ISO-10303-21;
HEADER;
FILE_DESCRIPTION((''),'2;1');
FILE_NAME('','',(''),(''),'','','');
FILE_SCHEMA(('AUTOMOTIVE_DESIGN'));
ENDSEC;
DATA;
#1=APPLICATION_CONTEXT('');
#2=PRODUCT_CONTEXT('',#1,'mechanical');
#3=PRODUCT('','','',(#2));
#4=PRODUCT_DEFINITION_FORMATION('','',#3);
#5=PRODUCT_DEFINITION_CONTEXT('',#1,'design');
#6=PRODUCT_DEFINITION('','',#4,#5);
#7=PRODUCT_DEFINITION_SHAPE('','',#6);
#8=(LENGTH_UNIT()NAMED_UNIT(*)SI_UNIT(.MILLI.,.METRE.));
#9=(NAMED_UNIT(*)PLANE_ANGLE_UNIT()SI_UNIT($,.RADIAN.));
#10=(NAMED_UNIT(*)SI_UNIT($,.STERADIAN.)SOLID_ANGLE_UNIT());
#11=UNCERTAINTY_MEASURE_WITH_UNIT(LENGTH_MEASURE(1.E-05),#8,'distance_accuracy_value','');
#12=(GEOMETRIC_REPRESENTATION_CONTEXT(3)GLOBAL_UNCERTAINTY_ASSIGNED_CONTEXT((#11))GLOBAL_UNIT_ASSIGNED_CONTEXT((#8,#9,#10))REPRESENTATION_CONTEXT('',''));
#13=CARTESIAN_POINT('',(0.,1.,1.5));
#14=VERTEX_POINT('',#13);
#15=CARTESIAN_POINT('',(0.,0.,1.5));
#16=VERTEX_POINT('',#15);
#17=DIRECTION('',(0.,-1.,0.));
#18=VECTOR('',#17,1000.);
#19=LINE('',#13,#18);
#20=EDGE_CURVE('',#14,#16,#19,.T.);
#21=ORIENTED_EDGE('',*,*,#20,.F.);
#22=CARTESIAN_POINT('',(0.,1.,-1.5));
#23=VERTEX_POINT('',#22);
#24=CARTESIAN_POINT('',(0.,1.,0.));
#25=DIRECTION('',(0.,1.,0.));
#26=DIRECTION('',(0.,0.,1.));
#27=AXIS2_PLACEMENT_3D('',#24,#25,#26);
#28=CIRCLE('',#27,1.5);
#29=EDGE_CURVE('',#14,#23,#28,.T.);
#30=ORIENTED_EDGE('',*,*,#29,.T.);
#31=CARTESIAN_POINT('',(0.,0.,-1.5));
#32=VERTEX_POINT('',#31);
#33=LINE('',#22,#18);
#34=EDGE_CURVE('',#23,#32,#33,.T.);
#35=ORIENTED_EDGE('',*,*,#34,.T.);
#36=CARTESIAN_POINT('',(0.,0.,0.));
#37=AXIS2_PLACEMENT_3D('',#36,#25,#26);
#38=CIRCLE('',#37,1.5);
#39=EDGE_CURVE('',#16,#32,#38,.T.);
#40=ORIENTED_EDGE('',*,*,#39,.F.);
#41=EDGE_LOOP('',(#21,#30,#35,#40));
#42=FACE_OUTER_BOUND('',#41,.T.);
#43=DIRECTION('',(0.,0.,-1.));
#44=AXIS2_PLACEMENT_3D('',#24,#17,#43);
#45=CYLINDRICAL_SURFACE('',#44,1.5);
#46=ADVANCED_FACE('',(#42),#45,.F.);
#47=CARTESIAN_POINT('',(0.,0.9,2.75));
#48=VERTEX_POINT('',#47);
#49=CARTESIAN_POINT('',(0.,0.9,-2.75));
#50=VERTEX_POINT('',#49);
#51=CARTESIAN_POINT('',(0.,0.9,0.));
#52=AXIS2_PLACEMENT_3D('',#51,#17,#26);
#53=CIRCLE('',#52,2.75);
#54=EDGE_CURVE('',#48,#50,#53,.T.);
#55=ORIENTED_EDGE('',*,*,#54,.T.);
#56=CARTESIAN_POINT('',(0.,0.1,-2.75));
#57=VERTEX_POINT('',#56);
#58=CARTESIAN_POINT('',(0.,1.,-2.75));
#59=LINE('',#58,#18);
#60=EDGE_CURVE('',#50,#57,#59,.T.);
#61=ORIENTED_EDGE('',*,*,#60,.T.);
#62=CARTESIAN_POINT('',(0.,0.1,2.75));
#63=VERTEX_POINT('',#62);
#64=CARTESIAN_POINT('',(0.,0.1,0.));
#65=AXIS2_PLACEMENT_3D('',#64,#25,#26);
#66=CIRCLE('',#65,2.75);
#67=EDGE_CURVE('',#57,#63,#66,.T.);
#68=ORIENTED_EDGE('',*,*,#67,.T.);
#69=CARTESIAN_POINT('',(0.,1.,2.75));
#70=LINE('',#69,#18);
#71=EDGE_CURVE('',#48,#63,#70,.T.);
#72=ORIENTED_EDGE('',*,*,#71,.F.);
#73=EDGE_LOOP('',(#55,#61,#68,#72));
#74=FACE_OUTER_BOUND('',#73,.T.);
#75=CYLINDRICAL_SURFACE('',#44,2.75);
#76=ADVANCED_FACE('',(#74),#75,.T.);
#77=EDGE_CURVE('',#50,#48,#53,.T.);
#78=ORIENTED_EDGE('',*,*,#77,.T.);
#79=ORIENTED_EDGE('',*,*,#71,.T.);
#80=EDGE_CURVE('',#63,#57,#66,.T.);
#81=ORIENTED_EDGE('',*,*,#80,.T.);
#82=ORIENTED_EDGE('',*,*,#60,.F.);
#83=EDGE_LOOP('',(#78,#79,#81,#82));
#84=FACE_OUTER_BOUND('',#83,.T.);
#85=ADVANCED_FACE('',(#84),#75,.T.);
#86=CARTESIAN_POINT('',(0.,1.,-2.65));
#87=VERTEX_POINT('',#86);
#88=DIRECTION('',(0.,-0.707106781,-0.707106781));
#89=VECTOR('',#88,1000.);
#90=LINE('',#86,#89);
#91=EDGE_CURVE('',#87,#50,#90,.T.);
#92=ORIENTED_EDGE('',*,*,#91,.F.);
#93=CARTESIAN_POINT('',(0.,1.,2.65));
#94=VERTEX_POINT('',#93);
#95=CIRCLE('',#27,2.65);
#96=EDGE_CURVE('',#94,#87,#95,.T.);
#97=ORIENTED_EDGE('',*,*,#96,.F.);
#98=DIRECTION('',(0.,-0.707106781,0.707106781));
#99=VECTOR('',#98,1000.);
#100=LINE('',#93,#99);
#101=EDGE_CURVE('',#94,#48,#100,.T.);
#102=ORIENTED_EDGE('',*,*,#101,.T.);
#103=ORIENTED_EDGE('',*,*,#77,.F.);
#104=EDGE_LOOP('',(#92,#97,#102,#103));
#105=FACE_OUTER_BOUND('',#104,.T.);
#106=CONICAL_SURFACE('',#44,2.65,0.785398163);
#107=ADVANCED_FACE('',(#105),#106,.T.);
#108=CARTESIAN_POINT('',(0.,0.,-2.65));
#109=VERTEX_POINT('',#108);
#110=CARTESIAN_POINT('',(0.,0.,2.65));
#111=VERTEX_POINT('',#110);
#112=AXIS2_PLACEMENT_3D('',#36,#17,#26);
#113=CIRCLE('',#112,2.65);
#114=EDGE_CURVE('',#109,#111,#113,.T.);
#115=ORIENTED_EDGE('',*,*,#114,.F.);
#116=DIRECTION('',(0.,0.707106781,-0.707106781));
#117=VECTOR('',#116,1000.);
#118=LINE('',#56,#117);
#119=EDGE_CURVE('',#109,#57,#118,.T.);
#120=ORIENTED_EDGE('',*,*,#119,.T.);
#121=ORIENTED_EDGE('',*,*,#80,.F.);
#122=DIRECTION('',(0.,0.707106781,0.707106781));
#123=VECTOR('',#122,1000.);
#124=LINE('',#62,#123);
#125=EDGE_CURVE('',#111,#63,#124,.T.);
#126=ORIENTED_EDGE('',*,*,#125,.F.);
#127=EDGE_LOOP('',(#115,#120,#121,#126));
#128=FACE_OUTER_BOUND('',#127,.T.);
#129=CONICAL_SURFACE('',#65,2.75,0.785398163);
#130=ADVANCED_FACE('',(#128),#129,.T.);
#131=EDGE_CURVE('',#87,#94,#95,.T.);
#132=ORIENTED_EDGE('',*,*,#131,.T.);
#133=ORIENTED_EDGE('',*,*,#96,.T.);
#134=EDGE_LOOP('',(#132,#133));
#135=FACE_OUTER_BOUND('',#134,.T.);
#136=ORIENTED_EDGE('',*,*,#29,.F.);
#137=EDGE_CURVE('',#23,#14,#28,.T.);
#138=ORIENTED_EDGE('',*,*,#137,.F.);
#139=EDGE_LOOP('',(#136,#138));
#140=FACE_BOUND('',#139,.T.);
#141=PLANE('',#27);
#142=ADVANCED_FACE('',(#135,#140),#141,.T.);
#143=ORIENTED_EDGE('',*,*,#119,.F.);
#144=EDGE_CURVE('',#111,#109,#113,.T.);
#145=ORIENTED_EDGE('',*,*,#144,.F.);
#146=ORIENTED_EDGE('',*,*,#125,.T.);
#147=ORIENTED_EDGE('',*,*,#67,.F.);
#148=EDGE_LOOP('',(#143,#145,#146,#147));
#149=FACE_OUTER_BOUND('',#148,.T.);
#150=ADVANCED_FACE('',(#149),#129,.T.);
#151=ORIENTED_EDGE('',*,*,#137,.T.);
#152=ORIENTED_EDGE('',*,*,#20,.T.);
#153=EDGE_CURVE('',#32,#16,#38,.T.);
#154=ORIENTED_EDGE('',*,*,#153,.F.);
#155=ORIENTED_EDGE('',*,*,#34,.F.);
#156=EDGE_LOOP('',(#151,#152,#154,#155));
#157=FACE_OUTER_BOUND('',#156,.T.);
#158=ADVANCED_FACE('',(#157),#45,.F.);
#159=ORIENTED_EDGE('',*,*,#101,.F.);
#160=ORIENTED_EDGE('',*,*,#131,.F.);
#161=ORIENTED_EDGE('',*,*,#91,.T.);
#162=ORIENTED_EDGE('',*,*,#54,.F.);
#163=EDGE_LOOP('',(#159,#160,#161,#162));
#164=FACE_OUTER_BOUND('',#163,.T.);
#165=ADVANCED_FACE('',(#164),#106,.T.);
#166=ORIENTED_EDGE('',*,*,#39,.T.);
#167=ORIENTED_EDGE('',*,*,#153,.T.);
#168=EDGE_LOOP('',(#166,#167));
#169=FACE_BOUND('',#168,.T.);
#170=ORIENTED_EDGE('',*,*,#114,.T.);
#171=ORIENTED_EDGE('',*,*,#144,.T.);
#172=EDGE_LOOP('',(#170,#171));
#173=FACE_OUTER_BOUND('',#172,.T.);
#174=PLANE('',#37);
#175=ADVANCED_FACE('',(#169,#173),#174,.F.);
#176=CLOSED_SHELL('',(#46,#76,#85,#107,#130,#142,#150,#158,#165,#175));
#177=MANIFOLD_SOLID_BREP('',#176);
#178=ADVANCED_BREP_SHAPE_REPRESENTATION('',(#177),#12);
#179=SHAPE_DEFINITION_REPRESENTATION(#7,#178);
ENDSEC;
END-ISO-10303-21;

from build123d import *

# Parameters (mm, degrees)
SKETCH1_R           = 2.75
SKETCH1_R_2         = 1.5
BOSS_EXTRUDE1_DEPTH = 1
CHAMFER1_SIZE       = 0.1


with BuildPart() as part:
    # Sketch1 → Boss-Extrude1 (new body)
    with BuildSketch(Plane(origin=(0, 0, 0), x_dir=(1, 0, 0), z_dir=(0, 1, 0))):
        with Locations(Location((0, 0, 0), (0, 0, 270))):
            Circle(SKETCH1_R)
        with Locations(Location((0, 0, 0), (0, 0, 270))):
            Circle(SKETCH1_R_2, mode=Mode.SUBTRACT)
    extrude(amount=BOSS_EXTRUDE1_DEPTH)

    # Chamfer1
    chamfer1_edges = [part.edges().sort_by_distance(p)[0] for p in [
        (0, 0, -2.75),
        (0, 1, -2.75),
    ]]
    chamfer(chamfer1_edges, length=CHAMFER1_SIZE)


solid = part.part
